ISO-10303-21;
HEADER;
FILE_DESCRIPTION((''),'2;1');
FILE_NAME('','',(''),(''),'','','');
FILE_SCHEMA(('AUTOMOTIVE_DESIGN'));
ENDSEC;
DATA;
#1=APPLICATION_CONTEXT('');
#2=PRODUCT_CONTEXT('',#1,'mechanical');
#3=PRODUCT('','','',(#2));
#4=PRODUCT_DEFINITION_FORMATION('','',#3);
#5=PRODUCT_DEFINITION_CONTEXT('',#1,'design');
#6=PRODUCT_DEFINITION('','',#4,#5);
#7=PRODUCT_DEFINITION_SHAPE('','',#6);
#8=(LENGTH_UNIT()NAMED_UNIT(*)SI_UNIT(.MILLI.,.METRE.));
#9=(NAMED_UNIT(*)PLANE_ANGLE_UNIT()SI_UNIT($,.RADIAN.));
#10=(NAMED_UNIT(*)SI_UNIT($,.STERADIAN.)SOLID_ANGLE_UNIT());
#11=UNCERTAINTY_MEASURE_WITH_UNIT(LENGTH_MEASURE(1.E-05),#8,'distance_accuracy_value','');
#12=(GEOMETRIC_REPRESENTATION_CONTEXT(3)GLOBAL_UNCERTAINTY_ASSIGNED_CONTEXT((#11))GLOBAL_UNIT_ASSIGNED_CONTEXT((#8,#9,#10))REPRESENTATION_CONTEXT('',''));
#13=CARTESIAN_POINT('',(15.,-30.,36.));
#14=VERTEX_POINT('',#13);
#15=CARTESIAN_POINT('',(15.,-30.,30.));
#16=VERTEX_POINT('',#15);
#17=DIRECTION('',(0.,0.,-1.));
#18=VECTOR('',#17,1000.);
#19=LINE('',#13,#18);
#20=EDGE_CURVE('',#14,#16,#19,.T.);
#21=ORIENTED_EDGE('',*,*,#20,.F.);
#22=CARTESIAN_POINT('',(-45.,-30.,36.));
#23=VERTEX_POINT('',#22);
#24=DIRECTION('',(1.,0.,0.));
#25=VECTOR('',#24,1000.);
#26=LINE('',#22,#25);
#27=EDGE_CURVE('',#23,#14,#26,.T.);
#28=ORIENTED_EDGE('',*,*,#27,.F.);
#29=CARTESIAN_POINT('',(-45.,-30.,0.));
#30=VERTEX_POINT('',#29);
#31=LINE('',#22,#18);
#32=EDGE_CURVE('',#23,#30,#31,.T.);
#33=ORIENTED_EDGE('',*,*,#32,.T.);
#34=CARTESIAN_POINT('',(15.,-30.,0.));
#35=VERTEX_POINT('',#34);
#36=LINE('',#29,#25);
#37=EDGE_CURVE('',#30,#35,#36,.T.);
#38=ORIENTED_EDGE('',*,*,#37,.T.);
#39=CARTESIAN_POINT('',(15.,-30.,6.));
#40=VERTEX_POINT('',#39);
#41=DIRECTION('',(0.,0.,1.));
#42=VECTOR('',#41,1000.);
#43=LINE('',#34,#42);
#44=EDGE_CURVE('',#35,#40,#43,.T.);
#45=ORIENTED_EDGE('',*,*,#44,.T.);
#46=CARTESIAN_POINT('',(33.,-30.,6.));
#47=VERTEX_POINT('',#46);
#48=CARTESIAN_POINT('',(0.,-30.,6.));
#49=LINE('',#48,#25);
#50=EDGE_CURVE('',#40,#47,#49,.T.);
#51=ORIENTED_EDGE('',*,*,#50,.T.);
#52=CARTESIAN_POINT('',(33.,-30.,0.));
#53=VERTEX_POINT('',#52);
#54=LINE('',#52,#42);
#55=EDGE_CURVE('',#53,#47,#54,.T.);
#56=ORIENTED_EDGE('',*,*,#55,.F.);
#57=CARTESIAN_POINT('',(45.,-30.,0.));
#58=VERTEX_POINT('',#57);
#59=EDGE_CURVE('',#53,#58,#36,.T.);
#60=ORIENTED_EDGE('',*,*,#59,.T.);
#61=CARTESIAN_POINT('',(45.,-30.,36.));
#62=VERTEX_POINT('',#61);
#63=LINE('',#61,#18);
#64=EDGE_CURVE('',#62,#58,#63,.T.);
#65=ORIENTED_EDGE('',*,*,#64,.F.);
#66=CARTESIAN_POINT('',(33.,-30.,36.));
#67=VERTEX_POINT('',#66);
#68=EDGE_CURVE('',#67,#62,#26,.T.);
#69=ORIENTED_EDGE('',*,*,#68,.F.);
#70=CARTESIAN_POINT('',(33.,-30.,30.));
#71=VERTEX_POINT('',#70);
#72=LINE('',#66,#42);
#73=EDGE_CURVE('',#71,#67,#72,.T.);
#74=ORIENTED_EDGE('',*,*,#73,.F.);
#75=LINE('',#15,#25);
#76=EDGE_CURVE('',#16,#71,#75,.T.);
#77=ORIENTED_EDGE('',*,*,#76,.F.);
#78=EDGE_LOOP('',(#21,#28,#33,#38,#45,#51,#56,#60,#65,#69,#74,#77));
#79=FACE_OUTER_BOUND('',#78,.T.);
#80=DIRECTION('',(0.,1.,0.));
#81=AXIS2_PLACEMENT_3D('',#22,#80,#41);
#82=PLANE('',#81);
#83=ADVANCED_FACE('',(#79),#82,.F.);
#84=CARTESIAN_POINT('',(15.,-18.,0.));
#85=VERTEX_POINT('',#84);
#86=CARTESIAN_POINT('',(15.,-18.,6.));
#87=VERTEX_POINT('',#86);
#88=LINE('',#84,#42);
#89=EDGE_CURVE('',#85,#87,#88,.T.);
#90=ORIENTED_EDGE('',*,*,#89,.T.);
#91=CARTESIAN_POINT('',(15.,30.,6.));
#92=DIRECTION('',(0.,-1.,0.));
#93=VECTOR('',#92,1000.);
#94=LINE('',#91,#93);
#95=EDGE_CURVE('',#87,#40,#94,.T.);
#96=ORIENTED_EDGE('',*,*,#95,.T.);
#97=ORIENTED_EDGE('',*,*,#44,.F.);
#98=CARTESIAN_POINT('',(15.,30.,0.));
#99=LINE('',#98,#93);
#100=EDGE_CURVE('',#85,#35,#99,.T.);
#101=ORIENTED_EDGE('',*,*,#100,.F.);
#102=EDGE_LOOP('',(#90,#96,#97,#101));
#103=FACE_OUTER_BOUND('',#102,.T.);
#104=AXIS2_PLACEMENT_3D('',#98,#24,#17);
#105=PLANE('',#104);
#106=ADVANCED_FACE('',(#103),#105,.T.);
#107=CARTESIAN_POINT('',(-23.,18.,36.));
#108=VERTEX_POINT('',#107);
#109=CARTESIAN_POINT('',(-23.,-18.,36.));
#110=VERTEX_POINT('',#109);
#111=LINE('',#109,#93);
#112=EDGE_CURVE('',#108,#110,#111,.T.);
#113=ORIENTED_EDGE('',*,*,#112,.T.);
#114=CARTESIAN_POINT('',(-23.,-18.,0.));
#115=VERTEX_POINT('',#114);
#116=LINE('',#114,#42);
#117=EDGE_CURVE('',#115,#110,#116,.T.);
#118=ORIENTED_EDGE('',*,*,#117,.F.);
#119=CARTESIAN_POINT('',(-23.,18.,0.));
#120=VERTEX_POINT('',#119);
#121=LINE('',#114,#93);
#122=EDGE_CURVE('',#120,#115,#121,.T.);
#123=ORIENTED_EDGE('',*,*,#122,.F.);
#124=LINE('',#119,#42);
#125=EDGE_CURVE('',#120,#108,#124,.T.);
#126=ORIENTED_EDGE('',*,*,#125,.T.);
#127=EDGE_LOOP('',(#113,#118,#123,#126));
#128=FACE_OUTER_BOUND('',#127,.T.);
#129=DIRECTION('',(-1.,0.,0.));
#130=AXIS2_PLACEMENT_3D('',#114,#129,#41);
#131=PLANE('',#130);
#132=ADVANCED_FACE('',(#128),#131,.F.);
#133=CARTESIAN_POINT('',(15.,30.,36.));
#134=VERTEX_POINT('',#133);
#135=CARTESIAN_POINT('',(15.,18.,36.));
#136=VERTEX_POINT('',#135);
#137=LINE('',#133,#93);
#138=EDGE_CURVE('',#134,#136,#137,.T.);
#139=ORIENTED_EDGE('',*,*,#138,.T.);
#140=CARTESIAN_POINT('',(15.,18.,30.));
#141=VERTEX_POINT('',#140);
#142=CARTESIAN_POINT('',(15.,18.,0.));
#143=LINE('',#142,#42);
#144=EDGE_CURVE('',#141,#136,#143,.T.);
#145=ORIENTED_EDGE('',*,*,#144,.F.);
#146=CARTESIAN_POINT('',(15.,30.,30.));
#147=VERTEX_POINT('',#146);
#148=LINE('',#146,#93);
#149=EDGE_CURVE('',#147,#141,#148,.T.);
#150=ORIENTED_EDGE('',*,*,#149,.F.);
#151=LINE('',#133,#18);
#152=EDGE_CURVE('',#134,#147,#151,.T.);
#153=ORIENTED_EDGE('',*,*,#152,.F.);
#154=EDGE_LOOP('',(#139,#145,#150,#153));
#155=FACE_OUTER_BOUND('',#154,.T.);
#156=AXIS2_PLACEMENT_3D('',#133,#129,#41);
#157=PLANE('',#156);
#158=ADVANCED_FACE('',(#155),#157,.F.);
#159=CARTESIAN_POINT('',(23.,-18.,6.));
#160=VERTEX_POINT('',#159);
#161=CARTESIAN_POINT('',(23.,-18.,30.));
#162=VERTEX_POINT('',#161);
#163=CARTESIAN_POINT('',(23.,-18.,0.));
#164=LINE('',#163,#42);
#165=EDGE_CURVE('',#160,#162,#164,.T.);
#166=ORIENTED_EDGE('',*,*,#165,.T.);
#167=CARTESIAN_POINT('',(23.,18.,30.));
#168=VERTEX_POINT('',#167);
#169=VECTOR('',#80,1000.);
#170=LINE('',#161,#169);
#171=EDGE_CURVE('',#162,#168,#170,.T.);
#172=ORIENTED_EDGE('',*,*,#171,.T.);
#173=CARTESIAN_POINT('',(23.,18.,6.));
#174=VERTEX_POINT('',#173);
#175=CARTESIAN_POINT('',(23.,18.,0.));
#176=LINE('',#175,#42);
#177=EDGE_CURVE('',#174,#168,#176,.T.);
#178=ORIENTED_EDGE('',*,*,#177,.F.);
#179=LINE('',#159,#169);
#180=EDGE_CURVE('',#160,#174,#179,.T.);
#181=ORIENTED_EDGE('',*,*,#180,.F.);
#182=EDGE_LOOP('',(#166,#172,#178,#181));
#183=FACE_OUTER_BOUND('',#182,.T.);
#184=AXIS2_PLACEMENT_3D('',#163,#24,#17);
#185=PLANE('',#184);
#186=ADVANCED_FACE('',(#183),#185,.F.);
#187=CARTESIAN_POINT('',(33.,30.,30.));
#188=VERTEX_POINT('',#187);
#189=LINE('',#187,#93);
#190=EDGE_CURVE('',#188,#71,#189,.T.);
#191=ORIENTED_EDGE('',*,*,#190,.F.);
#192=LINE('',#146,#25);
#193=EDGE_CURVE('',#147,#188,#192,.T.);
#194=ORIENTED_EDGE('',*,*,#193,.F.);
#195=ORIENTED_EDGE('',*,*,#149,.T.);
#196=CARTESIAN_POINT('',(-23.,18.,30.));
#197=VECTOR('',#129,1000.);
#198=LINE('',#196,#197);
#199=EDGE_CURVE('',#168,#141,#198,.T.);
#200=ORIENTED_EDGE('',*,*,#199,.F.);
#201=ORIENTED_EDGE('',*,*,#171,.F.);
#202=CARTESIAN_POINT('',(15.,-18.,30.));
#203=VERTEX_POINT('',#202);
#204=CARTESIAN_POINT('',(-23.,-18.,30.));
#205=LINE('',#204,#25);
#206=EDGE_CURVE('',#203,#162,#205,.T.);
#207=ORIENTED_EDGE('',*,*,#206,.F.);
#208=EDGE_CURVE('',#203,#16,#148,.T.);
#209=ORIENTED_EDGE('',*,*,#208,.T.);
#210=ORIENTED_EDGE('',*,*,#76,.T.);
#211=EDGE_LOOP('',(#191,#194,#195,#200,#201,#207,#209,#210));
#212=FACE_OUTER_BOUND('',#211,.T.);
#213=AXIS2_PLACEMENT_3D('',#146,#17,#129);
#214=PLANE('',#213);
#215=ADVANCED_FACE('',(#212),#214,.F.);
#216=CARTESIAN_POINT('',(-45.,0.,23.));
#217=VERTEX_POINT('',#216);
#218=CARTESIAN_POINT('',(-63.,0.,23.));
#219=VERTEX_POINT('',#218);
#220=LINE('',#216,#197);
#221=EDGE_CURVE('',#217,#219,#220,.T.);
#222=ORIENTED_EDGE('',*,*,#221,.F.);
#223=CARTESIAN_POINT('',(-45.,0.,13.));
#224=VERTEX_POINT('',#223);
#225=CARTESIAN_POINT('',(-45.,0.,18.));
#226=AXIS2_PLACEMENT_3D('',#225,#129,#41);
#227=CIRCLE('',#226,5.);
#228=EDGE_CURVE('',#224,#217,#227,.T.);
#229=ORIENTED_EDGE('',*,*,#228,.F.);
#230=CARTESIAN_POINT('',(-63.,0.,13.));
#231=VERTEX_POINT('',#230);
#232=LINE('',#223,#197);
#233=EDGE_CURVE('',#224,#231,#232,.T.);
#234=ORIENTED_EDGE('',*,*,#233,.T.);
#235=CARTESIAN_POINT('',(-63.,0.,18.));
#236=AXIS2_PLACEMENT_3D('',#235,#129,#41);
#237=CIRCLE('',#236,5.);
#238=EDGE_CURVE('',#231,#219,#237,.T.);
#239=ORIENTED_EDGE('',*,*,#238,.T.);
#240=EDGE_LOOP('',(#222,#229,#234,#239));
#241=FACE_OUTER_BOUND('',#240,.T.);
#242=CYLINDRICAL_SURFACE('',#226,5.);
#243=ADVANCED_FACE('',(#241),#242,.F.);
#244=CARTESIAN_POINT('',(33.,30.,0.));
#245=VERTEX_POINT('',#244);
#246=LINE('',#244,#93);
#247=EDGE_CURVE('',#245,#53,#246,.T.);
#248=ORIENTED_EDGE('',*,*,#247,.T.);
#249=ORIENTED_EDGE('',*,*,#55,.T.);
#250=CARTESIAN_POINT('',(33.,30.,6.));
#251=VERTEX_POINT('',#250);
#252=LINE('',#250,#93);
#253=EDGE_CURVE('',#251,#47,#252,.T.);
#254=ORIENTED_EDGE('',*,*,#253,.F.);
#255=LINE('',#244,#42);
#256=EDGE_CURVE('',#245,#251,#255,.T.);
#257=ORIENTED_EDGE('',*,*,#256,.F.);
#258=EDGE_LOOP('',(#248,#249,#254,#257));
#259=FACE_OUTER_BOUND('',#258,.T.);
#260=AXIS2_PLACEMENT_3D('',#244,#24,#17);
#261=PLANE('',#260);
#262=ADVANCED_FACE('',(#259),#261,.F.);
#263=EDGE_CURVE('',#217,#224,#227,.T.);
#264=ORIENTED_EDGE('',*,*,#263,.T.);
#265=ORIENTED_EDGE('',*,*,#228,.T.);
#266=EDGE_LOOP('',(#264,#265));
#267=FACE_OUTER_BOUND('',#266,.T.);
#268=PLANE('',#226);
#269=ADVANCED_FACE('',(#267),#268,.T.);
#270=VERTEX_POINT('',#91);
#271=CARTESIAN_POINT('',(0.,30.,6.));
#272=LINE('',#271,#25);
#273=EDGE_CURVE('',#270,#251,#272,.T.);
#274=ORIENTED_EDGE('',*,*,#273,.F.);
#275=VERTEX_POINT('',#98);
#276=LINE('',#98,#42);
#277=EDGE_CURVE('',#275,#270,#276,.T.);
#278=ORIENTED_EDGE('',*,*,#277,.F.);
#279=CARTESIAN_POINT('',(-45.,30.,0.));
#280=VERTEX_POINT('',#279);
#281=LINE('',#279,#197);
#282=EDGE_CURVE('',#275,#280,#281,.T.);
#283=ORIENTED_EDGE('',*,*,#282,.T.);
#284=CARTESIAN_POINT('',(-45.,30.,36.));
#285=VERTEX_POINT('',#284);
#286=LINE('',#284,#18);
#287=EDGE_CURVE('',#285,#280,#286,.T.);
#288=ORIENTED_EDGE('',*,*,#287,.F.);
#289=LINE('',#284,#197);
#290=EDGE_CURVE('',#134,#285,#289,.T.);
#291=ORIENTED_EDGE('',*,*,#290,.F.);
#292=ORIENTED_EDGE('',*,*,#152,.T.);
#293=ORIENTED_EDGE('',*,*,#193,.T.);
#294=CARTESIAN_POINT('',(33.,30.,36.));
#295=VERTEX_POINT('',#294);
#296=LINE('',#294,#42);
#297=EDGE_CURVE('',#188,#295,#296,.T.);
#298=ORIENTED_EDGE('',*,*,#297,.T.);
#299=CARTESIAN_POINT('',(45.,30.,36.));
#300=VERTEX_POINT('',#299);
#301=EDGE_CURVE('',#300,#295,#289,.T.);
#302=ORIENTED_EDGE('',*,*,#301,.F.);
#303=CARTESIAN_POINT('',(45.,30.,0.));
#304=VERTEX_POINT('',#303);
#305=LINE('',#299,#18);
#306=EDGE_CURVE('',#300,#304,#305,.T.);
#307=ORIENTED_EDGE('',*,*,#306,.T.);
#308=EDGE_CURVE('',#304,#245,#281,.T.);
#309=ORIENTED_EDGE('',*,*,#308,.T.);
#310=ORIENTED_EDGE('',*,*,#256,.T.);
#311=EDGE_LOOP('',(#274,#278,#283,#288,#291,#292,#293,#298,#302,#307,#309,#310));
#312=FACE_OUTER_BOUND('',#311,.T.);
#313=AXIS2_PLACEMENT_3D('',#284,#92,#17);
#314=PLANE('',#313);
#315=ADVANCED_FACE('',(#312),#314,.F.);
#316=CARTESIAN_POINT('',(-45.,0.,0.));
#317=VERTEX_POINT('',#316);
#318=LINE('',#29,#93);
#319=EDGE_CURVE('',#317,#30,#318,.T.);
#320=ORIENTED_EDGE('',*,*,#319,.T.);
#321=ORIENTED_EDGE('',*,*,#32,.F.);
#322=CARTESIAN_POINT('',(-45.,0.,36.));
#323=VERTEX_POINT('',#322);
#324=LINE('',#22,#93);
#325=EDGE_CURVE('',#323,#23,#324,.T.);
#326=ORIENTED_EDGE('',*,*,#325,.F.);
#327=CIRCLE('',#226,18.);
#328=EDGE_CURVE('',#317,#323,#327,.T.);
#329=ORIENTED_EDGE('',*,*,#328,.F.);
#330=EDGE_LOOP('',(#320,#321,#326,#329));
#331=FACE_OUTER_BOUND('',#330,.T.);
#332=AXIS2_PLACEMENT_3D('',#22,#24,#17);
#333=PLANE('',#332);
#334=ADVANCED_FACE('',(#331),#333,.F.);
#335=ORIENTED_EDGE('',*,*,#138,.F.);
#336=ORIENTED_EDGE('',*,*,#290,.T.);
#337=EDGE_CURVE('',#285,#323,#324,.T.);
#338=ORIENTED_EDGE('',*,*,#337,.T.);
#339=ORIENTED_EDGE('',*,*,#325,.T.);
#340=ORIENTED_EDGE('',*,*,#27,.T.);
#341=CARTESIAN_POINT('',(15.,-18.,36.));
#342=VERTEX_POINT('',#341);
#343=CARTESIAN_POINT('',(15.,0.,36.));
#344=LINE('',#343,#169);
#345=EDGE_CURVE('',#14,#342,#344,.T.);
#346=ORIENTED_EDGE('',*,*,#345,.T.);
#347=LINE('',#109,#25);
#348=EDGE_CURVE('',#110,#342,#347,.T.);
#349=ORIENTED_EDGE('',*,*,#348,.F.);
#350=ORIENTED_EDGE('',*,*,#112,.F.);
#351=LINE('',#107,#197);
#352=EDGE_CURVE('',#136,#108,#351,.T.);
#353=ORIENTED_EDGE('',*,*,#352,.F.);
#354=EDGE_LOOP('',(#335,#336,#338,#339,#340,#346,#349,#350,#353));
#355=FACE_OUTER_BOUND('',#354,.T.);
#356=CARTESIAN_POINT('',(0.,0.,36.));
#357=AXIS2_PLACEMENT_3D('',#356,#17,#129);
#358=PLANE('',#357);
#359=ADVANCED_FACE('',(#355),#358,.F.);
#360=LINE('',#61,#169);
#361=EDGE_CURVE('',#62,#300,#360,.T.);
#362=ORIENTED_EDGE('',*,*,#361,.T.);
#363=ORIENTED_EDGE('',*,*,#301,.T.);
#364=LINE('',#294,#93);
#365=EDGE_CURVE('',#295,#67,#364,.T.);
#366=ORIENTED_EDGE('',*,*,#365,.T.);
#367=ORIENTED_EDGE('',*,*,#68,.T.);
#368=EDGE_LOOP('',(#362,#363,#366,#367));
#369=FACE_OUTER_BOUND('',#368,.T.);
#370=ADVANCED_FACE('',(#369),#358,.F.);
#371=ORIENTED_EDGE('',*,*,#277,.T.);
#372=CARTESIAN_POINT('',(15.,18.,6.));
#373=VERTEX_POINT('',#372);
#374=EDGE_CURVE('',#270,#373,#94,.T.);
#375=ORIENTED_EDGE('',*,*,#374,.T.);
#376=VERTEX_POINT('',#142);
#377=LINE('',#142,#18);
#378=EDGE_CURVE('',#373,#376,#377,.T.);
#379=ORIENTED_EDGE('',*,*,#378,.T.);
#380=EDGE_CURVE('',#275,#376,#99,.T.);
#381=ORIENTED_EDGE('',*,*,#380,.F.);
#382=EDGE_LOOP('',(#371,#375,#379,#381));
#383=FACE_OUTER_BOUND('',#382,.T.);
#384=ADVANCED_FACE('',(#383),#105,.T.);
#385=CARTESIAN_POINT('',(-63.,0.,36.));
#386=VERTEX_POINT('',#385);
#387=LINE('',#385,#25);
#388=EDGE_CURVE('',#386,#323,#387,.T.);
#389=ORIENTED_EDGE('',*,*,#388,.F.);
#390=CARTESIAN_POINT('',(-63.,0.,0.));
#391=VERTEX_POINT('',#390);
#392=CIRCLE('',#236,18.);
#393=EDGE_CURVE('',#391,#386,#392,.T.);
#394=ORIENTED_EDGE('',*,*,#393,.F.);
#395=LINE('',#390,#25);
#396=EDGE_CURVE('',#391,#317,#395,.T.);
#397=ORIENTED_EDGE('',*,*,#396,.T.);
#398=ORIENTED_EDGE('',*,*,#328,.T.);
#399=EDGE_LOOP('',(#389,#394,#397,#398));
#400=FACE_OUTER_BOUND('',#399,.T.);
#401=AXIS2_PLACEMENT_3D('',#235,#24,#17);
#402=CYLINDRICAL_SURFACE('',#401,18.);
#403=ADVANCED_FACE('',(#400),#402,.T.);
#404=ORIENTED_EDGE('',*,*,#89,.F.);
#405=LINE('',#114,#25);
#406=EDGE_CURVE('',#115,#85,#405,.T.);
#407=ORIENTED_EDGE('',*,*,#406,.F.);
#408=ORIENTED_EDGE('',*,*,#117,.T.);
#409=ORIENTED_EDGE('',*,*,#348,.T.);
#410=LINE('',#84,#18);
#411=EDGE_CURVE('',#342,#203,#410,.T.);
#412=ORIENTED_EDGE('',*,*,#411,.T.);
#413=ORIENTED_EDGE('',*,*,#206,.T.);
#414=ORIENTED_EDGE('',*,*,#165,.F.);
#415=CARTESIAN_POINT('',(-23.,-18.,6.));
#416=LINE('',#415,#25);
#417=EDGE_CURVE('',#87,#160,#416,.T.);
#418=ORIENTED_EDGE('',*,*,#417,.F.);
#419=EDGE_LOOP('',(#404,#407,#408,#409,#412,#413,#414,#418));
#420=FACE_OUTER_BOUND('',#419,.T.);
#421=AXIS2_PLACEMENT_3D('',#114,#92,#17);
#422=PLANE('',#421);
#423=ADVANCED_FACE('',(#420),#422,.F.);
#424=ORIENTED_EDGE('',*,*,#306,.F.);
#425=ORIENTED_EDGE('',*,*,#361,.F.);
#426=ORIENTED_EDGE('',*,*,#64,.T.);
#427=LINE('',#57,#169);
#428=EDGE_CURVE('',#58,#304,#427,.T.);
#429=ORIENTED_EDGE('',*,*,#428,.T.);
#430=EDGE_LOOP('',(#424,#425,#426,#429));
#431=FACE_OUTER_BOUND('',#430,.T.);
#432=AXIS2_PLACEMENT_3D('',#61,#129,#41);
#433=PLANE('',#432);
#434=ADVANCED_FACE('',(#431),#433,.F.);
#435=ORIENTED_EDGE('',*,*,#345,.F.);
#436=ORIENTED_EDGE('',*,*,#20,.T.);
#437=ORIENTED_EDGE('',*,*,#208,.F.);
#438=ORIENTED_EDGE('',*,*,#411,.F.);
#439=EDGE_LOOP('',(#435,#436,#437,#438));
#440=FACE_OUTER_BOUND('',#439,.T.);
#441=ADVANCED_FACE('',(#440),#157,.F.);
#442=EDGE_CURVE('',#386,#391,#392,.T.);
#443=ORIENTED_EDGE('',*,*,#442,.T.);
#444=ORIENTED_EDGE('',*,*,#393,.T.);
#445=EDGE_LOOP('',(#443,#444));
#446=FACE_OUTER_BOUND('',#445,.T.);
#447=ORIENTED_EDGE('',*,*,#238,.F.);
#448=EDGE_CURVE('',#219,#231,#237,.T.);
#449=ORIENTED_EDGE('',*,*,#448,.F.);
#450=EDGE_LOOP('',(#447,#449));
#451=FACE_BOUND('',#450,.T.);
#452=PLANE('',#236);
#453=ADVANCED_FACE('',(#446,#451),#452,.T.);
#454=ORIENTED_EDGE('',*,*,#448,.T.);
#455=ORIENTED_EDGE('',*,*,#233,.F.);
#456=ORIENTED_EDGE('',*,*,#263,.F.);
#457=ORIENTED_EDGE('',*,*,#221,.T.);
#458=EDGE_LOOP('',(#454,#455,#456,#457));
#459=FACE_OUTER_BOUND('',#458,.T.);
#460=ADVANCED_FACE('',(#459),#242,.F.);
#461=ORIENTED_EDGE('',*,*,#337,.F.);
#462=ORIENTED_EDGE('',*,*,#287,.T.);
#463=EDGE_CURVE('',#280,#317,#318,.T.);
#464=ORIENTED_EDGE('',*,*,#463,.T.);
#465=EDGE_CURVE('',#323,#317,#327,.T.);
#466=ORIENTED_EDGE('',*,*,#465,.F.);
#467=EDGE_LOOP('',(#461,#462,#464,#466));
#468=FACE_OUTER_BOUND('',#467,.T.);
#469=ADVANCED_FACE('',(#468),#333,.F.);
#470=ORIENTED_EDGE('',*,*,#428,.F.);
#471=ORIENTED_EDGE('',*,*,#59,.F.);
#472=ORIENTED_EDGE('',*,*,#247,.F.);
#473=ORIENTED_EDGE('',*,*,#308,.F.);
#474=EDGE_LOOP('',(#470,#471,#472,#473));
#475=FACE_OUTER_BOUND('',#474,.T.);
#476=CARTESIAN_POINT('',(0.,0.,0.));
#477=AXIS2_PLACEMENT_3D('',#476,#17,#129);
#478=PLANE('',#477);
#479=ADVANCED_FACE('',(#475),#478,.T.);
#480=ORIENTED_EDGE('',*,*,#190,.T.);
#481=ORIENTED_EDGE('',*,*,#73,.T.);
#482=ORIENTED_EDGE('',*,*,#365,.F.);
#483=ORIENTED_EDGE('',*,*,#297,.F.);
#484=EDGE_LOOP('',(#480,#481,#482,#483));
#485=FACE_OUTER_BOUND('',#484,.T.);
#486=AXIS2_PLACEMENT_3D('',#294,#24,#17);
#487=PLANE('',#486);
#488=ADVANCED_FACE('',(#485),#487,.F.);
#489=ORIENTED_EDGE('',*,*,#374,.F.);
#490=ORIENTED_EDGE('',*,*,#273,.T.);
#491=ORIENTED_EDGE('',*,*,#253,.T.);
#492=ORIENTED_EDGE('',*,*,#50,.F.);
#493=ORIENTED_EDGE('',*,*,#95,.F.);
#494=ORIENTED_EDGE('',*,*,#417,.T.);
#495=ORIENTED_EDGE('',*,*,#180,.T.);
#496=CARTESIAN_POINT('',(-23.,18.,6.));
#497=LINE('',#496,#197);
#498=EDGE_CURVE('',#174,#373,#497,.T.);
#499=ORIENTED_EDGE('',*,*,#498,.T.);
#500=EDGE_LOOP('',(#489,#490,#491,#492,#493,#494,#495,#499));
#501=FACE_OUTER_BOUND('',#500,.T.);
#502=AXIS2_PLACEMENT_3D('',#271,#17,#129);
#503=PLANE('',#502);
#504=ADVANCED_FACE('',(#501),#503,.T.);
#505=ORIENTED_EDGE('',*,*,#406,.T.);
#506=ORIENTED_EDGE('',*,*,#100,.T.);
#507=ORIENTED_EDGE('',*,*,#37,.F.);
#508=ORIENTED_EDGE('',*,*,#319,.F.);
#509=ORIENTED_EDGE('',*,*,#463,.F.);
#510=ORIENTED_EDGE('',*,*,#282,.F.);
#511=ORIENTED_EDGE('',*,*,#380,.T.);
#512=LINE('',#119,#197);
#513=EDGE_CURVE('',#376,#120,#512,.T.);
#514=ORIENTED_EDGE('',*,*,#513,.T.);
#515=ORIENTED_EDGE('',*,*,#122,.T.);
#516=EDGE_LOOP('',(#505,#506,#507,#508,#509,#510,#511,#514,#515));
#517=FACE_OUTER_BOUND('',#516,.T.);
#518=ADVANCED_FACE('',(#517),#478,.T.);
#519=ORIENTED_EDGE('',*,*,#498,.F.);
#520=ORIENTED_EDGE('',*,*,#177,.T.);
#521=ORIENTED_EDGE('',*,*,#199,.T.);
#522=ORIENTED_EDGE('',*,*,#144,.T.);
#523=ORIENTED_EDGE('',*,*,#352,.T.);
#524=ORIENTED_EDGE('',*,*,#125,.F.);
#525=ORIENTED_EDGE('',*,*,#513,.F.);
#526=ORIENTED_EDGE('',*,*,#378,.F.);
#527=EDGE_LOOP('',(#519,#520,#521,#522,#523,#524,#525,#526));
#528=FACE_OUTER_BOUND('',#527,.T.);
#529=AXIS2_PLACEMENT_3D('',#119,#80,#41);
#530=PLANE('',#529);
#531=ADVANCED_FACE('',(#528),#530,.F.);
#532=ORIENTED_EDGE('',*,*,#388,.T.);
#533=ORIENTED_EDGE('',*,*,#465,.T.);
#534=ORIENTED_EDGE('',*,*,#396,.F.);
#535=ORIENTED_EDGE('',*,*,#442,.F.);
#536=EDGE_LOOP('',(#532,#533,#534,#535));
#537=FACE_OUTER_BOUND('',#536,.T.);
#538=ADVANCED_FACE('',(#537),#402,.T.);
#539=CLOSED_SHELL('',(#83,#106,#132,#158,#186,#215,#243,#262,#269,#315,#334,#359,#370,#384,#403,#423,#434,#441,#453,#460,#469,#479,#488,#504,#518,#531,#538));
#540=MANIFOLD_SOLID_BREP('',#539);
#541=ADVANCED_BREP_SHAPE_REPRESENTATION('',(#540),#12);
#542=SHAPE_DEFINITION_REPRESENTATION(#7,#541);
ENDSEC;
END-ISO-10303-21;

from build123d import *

# Parameters (mm, degrees)
BASE_BLOCK_SKETCH_W        = 90
BASE_BLOCK_SKETCH_H        = 60
BASE_BLOCK_DEPTH           = 36
WINDOW_SKETCH_W            = 46
WINDOW_SKETCH_H            = 36
THROUGH_WINDOW_46X36_DEPTH = 36
BOSS_SKETCH_R              = 18
CYLINDRICAL_BOSS_DEPTH     = 18
BOSS_BORE_SKETCH_R         = 5
BOSS_BORE_DEPTH            = 18
TOP_NOTCHES_SKETCH_W       = 18
TOP_NOTCHES_SKETCH_H       = 6
TOP_NOTCHES_DEPTH          = 95.154128959
END_NOTCH_SKETCH_W         = 18
END_NOTCH_SKETCH_H         = 6
END_NOTCH_DEPTH            = 95.154128959


with BuildPart() as part:
    # Base Block Sketch → Base Block (new body)
    with BuildSketch(Plane.XY):
        Rectangle(BASE_BLOCK_SKETCH_W, BASE_BLOCK_SKETCH_H)
    extrude(amount=BASE_BLOCK_DEPTH)

    # Window Sketch → Through Window 46x36 (cut)
    with BuildSketch(Plane.XY.offset(36)):
        Rectangle(WINDOW_SKETCH_W, WINDOW_SKETCH_H)
    extrude(amount=-THROUGH_WINDOW_46X36_DEPTH, mode=Mode.SUBTRACT)

    # Boss Sketch → Cylindrical Boss (add)
    with BuildSketch(Plane.ZY.offset(45)):
        with Locations((18, 0)):
            Circle(BOSS_SKETCH_R)
    extrude(amount=CYLINDRICAL_BOSS_DEPTH)

    # Boss Bore Sketch → Boss Bore (cut)
    with BuildSketch(Plane.ZY.offset(63)):
        with Locations((18, 0)):
            Circle(BOSS_BORE_SKETCH_R)
    extrude(amount=-BOSS_BORE_DEPTH, mode=Mode.SUBTRACT)

    # Top Notches Sketch → Top Notches (cut, through all)
    with BuildSketch(Plane.XZ.offset(30)):
        with Locations((24, 3)):
            Rectangle(TOP_NOTCHES_SKETCH_W, TOP_NOTCHES_SKETCH_H)
    extrude(amount=-TOP_NOTCHES_DEPTH, mode=Mode.SUBTRACT)

    # End Notch Sketch → End Notch (cut, through all)
    with BuildSketch(Plane.XZ.offset(30)):
        with Locations((24, 33)):
            Rectangle(END_NOTCH_SKETCH_W, END_NOTCH_SKETCH_H)
    extrude(amount=-END_NOTCH_DEPTH, mode=Mode.SUBTRACT)


solid = part.part
